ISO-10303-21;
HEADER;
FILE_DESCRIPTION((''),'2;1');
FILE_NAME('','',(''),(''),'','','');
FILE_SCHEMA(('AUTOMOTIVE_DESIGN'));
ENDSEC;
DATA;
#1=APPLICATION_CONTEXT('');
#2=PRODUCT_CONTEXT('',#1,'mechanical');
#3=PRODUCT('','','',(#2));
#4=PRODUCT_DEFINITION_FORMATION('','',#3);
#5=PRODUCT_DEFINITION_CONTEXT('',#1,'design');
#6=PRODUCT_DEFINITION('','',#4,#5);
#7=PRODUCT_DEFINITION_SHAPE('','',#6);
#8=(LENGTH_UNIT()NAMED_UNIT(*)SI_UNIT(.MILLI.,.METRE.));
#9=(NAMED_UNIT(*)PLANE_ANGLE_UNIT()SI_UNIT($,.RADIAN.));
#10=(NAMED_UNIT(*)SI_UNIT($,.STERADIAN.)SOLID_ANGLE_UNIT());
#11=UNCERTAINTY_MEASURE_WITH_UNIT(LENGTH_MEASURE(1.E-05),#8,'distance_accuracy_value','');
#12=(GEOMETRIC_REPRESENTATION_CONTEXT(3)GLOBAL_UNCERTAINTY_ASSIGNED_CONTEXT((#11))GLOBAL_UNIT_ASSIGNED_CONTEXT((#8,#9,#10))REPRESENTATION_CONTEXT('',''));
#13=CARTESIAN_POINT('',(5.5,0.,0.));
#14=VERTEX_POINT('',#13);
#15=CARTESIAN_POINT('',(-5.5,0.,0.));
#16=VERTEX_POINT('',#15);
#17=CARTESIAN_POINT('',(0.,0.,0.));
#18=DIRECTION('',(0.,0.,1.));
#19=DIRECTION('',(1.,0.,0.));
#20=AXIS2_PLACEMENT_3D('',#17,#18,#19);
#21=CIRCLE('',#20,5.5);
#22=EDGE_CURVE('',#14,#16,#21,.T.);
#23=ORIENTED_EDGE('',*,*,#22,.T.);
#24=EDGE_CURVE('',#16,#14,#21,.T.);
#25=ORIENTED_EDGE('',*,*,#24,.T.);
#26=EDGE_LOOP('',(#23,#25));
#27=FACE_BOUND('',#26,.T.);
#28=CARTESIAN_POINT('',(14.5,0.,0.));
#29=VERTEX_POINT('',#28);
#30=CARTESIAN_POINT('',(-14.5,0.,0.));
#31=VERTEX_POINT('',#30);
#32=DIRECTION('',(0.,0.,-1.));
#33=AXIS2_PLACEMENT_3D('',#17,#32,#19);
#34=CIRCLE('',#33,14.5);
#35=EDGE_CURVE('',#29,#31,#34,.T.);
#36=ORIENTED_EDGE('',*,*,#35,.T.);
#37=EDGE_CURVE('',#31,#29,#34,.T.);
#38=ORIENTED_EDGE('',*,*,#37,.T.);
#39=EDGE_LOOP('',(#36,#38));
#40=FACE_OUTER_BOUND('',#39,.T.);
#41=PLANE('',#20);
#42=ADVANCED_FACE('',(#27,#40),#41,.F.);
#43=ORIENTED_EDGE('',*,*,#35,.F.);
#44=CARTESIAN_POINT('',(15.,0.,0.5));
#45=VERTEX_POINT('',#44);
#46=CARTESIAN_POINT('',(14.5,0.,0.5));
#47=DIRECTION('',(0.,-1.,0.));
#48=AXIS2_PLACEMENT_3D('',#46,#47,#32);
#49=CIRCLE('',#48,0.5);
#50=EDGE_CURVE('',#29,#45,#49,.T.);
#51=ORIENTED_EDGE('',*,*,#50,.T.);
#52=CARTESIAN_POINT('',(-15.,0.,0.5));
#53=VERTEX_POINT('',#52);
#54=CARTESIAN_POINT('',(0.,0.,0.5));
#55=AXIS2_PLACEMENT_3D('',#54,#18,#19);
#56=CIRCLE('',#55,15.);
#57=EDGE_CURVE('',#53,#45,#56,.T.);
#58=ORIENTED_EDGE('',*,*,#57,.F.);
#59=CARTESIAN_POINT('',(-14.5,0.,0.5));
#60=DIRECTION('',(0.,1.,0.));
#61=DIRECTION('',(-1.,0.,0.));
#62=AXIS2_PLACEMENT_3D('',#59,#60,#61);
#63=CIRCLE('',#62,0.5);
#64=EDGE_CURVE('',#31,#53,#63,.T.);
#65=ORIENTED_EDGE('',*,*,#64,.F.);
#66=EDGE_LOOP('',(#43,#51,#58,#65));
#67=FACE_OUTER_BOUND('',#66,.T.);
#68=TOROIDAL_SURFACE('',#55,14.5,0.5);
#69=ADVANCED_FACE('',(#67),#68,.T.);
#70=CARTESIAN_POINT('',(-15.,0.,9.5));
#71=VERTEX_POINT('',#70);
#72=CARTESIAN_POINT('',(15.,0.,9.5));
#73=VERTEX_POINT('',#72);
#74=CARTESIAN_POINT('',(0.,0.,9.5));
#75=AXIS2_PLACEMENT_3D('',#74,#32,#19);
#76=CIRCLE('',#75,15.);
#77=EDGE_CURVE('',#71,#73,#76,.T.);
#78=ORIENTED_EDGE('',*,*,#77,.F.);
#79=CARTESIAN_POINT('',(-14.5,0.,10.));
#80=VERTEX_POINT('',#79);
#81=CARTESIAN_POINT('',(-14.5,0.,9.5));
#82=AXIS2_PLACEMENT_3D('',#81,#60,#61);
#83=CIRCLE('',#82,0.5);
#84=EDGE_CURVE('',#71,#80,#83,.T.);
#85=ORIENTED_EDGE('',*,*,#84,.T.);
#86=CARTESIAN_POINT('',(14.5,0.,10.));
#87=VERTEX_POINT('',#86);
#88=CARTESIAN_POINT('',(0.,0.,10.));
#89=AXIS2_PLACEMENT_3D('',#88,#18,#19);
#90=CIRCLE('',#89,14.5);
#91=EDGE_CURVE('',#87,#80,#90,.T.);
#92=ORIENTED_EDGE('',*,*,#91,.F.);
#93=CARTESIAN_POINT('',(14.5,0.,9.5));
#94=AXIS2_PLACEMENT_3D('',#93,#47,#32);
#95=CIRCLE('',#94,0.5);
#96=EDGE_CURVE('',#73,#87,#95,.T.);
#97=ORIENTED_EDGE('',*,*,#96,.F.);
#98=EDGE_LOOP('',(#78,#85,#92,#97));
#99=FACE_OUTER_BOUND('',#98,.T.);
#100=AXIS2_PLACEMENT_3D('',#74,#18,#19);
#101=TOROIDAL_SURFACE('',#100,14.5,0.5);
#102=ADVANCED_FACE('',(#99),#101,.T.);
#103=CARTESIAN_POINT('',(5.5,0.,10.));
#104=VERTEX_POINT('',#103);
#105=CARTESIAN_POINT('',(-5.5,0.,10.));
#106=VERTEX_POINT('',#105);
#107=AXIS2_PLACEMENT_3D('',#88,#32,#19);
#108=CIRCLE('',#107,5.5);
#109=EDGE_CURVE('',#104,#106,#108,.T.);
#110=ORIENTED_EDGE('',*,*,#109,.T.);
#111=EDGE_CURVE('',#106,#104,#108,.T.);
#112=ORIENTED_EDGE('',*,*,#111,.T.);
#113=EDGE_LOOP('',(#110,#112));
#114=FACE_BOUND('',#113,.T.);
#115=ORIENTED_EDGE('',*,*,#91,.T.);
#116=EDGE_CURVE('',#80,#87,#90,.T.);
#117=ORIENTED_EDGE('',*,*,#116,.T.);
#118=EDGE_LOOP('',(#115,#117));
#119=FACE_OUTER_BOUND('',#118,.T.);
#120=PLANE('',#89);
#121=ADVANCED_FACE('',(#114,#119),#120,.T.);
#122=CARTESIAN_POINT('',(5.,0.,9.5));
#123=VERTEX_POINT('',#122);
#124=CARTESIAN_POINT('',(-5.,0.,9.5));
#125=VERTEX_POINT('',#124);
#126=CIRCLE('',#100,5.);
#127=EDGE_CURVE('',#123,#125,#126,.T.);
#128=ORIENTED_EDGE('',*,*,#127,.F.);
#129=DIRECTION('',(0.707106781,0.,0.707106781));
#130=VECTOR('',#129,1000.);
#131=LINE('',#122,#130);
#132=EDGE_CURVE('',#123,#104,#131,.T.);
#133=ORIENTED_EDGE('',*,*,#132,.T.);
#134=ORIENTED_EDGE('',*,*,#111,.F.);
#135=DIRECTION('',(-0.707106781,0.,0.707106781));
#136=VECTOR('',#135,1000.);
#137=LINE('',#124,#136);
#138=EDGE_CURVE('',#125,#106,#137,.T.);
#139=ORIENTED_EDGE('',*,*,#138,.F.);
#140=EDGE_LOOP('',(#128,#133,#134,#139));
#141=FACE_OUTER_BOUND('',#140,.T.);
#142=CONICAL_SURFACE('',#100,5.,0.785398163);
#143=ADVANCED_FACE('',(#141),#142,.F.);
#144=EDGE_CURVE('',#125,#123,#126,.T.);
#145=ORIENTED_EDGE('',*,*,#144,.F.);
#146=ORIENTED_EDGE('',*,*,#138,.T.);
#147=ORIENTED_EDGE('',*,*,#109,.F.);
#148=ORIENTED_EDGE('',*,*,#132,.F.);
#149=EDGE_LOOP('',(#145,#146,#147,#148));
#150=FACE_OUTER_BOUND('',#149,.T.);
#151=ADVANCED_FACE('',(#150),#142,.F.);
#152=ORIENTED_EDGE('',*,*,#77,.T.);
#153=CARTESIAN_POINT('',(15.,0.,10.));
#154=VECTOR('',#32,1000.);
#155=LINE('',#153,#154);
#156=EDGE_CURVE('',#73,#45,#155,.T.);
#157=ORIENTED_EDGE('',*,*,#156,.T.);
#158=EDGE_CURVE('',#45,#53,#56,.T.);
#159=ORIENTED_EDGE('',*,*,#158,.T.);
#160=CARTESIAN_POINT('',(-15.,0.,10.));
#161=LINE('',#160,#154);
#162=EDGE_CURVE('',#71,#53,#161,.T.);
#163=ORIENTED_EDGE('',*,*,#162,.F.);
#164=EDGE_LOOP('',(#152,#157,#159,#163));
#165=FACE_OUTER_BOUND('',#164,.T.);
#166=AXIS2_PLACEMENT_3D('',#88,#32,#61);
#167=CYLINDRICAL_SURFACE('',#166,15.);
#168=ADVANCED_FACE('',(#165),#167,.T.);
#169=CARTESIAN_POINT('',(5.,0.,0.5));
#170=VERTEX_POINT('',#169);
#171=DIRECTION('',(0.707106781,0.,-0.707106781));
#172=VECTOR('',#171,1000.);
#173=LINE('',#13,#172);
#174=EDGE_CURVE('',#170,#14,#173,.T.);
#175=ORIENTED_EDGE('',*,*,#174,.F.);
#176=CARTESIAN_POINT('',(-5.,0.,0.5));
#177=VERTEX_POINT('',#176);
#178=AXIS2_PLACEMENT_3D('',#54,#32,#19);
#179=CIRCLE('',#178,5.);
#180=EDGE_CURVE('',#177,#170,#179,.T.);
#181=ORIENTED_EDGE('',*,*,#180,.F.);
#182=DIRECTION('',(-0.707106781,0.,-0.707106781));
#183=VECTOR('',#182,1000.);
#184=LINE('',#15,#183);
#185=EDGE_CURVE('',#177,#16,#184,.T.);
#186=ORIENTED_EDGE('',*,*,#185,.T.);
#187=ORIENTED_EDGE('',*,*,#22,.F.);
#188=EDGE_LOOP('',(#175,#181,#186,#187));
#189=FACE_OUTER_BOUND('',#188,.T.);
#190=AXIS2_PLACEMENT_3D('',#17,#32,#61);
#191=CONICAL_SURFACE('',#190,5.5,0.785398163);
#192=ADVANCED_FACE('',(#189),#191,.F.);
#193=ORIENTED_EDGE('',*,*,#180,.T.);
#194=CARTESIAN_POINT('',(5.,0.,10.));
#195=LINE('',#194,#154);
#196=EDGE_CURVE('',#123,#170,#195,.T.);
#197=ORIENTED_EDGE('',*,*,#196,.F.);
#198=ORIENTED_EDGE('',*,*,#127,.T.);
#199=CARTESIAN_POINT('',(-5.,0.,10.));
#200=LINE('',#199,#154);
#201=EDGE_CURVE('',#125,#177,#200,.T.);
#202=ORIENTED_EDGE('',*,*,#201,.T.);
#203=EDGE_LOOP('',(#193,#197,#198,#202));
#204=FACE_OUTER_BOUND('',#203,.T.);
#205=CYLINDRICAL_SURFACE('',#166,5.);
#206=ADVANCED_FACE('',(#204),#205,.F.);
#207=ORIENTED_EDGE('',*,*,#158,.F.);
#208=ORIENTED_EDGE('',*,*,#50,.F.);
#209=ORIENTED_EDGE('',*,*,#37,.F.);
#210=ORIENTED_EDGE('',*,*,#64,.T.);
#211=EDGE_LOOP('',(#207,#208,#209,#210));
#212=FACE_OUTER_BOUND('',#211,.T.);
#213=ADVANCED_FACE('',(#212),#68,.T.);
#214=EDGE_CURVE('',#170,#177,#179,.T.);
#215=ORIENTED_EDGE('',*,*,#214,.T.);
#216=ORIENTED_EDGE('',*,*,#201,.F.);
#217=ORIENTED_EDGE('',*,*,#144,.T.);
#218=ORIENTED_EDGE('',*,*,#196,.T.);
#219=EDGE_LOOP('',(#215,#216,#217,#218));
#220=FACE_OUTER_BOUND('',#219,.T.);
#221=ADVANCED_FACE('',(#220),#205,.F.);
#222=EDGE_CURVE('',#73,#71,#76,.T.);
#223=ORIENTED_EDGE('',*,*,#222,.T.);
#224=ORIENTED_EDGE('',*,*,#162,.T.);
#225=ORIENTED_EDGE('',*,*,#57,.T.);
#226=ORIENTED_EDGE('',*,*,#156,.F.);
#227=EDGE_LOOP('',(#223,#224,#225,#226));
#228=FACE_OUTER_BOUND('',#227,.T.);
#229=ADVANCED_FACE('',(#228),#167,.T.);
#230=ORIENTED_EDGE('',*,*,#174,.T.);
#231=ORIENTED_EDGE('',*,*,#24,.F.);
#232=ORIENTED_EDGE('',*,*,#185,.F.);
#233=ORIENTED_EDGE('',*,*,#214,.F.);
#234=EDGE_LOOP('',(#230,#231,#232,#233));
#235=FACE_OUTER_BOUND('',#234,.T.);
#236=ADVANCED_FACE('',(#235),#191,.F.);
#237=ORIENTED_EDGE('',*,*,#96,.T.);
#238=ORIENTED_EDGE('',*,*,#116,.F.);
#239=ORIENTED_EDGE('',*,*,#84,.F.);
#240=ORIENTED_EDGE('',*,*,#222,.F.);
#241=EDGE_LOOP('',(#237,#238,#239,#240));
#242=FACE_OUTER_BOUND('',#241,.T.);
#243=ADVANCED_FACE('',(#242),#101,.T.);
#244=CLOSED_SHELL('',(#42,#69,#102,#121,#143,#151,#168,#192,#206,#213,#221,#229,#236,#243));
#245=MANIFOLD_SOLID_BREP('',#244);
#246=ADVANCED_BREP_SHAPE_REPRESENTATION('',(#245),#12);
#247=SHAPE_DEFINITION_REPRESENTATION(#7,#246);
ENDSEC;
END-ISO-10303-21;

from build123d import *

# Parameters (mm, degrees)
SKETCH_1_R      = 15
SKETCH_1_R_2    = 5
EXTRUDE_1_DEPTH = 10
FILLET_1_R      = 0.5
CHAMFER_1_SIZE  = 0.5


with BuildPart() as part:
    # 草图1 → 凸台-拉伸1 (new body)
    with BuildSketch(Plane.XY):
        Circle(SKETCH_1_R)
        Circle(SKETCH_1_R_2, mode=Mode.SUBTRACT)
    extrude(amount=EXTRUDE_1_DEPTH)

    # 圆角1
    fillet_1_edges = [part.edges().sort_by_distance(p)[0] for p in [
        (-15, 0, 0),
        (-15, 0, 10),
    ]]
    fillet(fillet_1_edges, radius=FILLET_1_R)

    # 倒角1
    chamfer_1_edges = [part.edges().sort_by_distance(p)[0] for p in [
        (-5, 0, 0),
        (-5, 0, 10),
    ]]
    chamfer(chamfer_1_edges, length=CHAMFER_1_SIZE)


solid = part.part
